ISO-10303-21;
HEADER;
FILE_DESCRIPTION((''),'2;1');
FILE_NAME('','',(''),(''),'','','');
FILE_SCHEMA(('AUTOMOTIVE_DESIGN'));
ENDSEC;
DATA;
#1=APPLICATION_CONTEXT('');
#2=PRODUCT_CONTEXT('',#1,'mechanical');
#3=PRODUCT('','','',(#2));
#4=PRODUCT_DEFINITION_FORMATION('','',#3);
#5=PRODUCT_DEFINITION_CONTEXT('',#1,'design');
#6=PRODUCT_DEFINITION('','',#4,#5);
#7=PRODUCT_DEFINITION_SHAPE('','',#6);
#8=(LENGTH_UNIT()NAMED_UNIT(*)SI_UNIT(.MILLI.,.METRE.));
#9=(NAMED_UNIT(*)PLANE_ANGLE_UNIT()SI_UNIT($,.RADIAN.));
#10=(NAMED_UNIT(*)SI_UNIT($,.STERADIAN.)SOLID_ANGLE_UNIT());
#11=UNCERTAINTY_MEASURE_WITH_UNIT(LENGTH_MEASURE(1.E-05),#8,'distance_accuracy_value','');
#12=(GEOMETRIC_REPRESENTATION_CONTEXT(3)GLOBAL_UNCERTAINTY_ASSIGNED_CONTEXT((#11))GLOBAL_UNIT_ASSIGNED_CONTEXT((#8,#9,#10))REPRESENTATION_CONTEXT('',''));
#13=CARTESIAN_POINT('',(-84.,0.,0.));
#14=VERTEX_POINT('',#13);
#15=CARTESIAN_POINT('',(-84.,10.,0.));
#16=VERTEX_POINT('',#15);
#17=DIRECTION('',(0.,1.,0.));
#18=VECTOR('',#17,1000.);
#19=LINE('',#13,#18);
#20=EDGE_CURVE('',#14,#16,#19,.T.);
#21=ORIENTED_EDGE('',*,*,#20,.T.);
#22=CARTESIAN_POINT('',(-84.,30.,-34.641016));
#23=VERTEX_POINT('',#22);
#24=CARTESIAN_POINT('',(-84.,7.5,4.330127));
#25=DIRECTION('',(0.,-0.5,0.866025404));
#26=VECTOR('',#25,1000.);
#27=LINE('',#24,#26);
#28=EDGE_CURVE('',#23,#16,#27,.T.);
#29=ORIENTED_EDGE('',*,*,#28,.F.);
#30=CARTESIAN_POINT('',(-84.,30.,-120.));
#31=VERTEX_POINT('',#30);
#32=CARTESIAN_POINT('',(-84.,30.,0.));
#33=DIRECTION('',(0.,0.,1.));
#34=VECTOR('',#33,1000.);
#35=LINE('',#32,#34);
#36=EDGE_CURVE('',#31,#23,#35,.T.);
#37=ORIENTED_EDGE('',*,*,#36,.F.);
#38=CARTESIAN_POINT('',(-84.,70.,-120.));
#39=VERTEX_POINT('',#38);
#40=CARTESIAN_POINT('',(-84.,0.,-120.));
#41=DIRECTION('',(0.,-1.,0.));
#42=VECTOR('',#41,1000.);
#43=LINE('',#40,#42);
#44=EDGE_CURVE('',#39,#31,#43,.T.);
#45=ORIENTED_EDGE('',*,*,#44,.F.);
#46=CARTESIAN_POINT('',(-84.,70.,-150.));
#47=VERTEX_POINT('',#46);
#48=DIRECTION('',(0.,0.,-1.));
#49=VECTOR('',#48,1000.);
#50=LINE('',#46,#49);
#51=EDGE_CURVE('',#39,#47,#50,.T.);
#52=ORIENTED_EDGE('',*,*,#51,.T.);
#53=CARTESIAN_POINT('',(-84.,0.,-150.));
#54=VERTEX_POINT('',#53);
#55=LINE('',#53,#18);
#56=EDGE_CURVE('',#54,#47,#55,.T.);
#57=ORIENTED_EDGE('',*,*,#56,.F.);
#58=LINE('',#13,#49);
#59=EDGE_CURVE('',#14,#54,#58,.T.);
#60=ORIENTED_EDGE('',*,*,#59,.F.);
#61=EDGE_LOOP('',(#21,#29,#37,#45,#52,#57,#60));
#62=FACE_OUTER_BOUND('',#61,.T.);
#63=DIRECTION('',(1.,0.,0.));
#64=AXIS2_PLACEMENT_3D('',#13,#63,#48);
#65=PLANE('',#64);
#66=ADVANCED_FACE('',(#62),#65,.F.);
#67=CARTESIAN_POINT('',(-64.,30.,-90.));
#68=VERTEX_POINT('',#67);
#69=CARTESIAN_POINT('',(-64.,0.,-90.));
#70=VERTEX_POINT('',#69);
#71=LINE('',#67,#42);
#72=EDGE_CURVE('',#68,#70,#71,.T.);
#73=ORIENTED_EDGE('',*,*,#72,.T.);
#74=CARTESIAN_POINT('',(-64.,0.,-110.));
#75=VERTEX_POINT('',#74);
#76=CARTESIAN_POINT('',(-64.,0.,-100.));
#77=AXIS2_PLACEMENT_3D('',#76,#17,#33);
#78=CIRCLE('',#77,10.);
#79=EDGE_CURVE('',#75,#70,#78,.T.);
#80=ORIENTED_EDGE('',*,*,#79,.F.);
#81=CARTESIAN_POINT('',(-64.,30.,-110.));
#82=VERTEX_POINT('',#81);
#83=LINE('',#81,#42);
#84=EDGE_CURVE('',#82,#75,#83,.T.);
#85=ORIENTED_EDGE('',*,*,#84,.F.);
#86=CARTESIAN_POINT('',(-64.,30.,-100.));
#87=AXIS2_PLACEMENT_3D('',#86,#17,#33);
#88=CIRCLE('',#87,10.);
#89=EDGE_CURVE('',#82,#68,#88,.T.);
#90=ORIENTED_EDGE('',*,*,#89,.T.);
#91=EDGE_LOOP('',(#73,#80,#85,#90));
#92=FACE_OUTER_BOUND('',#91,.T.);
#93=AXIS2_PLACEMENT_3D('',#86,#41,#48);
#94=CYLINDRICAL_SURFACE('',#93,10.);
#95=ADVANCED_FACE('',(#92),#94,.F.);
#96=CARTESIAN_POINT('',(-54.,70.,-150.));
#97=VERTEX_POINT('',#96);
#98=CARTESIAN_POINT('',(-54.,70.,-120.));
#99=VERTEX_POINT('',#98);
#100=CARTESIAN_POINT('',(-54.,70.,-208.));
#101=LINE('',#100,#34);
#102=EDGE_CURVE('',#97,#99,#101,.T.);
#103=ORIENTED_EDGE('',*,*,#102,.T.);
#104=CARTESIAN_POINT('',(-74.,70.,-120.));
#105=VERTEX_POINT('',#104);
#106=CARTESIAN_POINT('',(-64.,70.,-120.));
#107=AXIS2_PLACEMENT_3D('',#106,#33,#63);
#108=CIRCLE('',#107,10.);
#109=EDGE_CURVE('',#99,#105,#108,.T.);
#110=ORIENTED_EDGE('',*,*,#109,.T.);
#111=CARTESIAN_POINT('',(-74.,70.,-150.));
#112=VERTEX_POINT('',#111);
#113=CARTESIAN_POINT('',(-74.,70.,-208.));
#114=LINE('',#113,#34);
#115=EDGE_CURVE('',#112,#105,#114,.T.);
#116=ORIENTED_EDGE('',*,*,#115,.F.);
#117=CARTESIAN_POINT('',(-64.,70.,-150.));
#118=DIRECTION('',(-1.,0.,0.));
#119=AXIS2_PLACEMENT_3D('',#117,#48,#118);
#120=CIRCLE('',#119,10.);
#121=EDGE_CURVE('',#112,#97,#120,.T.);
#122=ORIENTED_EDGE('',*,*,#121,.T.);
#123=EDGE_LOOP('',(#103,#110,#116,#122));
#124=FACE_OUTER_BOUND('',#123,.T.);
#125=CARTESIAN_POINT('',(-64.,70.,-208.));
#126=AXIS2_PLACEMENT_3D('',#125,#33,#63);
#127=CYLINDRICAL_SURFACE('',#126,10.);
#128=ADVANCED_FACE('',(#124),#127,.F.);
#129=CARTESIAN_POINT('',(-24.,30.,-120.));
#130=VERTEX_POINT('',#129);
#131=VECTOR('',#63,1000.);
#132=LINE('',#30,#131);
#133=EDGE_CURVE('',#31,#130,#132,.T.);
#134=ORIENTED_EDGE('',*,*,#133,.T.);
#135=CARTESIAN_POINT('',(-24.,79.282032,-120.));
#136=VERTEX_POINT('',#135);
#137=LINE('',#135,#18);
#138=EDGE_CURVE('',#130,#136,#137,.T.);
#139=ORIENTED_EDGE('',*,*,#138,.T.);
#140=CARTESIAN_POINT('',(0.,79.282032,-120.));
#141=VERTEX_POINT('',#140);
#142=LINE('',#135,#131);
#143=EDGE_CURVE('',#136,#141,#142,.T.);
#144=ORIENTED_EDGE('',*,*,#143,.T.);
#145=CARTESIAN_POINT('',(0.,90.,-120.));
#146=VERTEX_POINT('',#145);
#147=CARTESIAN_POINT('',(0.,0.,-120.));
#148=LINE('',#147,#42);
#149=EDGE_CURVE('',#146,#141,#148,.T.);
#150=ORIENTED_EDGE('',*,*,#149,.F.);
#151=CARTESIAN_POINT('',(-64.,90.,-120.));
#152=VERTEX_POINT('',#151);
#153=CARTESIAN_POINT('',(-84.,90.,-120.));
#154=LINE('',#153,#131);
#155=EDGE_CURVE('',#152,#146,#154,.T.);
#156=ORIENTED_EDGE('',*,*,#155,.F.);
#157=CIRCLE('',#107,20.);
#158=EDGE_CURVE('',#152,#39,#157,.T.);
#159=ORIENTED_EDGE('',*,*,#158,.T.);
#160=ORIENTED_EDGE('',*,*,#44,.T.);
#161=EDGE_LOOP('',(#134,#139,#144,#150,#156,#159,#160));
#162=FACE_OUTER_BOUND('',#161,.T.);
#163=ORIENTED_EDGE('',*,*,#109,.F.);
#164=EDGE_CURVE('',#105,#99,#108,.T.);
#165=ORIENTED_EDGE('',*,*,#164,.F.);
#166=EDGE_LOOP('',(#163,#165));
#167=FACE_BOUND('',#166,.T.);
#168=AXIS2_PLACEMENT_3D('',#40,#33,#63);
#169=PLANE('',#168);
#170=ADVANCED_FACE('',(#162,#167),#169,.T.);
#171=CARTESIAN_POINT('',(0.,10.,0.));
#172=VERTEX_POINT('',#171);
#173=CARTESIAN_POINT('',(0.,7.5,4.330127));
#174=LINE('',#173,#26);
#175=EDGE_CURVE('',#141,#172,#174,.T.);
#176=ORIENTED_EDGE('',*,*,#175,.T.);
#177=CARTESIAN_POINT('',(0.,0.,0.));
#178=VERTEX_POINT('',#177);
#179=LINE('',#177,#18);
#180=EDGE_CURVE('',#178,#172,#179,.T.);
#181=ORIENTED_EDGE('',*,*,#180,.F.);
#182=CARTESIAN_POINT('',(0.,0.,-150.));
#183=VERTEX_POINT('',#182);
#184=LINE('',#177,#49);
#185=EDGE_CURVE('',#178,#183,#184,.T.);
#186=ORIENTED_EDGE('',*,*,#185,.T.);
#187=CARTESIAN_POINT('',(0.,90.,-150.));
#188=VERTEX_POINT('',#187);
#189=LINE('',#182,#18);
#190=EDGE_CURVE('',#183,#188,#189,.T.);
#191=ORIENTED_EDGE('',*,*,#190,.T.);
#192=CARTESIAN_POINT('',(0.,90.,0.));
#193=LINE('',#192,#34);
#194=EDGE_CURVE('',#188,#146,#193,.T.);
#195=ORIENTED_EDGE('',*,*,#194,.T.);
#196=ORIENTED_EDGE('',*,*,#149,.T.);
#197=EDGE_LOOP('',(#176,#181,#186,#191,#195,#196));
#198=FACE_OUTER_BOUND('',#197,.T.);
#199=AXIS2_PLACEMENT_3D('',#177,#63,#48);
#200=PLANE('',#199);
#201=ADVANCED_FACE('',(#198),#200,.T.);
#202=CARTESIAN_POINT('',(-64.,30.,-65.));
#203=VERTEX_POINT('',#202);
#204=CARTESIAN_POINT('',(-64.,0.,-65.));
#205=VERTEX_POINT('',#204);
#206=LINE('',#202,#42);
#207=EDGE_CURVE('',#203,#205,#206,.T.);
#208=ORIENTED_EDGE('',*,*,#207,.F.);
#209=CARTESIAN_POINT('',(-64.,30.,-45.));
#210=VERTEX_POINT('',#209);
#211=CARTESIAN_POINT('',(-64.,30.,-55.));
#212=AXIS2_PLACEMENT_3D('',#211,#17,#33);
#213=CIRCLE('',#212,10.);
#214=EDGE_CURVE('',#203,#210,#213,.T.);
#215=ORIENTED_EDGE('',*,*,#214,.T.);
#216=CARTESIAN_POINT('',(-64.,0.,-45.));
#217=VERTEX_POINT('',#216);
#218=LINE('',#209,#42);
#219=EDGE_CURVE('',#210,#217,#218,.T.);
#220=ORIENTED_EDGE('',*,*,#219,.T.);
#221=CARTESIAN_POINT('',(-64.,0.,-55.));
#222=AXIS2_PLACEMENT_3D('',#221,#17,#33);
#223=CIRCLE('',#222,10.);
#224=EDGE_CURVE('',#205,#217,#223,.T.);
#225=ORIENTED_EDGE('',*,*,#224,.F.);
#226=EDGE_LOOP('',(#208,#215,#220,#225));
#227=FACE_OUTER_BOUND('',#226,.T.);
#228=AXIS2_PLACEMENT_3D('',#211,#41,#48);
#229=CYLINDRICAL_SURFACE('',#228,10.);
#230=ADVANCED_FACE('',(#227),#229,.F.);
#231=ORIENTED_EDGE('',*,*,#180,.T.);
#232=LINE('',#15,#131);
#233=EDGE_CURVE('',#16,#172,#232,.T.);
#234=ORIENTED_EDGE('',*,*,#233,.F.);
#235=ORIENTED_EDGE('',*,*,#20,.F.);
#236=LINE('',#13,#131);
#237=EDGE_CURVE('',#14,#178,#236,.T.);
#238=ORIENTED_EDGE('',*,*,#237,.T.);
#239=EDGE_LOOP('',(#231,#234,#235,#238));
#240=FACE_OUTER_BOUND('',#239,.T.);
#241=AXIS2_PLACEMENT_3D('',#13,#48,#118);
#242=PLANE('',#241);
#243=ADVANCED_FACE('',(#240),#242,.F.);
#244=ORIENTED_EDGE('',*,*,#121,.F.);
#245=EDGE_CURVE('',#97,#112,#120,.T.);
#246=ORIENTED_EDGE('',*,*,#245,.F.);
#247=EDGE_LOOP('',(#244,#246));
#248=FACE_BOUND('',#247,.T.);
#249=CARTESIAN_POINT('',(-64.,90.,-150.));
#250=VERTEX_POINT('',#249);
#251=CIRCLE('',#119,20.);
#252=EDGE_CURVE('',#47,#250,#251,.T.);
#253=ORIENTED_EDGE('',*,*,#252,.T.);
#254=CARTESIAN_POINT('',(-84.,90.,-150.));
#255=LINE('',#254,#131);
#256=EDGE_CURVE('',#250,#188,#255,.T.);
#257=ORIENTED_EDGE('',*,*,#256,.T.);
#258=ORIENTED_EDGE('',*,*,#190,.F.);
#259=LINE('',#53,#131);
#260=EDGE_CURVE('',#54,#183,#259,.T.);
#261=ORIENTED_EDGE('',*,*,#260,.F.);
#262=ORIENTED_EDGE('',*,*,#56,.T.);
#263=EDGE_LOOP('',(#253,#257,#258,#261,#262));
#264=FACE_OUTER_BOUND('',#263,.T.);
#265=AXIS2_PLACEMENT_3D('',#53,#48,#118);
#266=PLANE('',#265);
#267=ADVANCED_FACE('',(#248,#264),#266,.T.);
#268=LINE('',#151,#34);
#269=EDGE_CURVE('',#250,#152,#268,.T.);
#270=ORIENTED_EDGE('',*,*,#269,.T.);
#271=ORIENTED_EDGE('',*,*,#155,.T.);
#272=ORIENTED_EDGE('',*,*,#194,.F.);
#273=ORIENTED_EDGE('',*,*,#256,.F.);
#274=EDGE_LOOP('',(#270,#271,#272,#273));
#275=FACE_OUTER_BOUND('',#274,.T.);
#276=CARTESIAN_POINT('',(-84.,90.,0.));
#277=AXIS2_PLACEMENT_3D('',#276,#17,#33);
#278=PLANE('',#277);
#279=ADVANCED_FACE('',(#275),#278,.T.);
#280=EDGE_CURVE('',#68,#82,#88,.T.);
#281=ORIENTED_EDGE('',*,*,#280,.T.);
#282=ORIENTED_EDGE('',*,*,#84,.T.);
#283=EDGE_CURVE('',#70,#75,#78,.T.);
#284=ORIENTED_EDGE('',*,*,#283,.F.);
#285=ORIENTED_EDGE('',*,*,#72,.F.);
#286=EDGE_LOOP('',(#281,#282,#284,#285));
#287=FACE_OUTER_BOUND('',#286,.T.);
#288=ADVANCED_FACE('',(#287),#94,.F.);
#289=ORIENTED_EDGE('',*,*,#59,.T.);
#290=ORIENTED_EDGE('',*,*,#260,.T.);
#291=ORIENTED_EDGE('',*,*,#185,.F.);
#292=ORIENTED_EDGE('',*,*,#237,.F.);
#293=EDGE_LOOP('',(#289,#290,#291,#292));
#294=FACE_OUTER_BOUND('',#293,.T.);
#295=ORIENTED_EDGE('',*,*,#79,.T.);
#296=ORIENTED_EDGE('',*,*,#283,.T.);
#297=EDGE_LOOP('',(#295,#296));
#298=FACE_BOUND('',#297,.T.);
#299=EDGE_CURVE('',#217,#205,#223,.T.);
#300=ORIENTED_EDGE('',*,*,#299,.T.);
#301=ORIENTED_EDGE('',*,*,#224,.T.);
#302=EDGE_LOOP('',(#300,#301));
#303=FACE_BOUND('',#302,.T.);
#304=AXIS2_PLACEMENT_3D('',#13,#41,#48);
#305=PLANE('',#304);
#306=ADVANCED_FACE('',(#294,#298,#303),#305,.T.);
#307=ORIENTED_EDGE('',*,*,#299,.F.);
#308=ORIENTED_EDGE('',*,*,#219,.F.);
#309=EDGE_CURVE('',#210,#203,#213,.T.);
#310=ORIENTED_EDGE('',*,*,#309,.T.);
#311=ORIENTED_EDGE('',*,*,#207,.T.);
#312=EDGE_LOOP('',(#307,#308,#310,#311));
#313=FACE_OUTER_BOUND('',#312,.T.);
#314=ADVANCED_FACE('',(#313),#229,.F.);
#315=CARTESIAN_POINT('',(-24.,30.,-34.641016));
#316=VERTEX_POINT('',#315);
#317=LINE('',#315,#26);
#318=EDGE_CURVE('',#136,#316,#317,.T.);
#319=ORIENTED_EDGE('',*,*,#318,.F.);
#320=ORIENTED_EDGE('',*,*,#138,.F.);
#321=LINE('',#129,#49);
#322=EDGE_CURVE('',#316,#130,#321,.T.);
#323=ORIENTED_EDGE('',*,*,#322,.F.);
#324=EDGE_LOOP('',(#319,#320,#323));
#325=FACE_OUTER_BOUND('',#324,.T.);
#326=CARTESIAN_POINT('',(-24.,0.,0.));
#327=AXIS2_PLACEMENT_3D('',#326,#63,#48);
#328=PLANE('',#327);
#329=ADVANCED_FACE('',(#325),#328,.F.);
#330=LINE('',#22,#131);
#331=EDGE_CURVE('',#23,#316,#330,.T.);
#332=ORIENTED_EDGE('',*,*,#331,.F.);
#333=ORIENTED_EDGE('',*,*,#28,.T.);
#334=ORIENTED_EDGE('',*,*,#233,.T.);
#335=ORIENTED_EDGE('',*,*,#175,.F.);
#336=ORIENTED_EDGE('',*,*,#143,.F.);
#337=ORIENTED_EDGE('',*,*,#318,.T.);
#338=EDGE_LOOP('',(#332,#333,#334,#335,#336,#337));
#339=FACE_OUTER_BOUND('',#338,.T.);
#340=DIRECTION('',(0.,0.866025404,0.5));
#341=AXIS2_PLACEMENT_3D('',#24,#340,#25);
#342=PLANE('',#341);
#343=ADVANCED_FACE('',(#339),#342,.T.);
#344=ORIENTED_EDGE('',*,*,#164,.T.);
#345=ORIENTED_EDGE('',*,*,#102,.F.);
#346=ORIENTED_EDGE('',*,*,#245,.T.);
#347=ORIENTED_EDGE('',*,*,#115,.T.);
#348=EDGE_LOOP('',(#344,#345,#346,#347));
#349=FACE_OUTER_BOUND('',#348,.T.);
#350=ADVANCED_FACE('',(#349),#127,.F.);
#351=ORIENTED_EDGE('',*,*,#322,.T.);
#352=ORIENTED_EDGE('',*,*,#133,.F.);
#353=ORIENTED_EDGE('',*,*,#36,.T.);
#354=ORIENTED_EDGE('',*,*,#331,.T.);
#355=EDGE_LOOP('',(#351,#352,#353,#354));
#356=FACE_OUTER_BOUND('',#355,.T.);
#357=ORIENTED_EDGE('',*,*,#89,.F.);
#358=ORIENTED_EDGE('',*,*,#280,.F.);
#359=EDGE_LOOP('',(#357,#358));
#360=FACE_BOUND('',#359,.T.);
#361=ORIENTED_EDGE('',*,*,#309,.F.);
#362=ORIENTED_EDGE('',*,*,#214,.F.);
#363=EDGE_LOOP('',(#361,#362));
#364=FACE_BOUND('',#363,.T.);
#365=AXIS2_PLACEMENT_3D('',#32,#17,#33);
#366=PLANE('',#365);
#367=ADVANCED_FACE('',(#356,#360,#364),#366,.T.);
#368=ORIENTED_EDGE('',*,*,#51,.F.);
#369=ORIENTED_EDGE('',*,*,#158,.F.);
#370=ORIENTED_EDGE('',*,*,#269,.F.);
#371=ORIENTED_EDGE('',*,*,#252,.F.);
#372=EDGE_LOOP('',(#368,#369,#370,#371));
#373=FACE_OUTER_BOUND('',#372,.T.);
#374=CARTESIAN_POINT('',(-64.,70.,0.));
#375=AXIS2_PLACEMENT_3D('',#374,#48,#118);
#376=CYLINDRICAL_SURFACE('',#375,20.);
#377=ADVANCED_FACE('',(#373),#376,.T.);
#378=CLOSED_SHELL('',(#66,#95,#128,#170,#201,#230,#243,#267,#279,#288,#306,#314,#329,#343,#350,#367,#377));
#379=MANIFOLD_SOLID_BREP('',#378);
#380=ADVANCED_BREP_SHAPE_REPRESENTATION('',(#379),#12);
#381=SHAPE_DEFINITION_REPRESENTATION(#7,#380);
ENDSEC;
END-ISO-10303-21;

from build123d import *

# Parameters (mm, degrees)
BRACKET_BODY_DEPTH     = 84
GUSSET_DEPTH           = 24
BASE_HOLES_SKETCH_R    = 10
BASE_HOLES_2X_20_DEPTH = 30
LUG_HOLE_SKETCH_R      = 10
LUG_HOLE_20_DEPTH      = 208
LUG_TOP_FILLET_R20_R   = 20


with BuildPart() as part:
    # Bracket Profile Sketch → Bracket Body (new body)
    with BuildSketch(Plane(origin=(0, 0, 0), x_dir=(0, 0, -1), z_dir=(1, 0, 0))):
        Polygon((0, 10), (0, 0), (150, 0), (150, 90), (120, 90), (120, 79.282032303), (120, 70), (120, 30), (34.641016151, 30), align=None)
    extrude(amount=-BRACKET_BODY_DEPTH)

    # Gusset Sketch → Gusset (add)
    with BuildSketch(Plane(origin=(0, 0, 0), x_dir=(0, 0, -1), z_dir=(1, 0, 0))):
        Polygon((34.641016151, 30), (120, 79.282032303), (120, 30), align=None)
    extrude(amount=-GUSSET_DEPTH)

    # Base Holes Sketch → Base Holes 2xØ20 (cut)
    with BuildSketch(Plane(origin=(0, 0, 0), x_dir=(1, 0, 0), z_dir=(0, 1, 0))):
        with Locations(Location((-64, 100, 0), (0, 0, 270))):
            Circle(BASE_HOLES_SKETCH_R)
        with Locations(Location((-64, 55, 0), (0, 0, 270))):
            Circle(BASE_HOLES_SKETCH_R)
    extrude(amount=BASE_HOLES_2X_20_DEPTH, mode=Mode.SUBTRACT)

    # Lug Hole Sketch → Lug Hole Ø20 (cut)
    with BuildSketch(Plane.XY):
        with Locations((-64, 70)):
            Circle(LUG_HOLE_SKETCH_R)
    extrude(amount=-LUG_HOLE_20_DEPTH, mode=Mode.SUBTRACT)

    # Lug Top Fillet R20
    lug_top_fillet_r20_edges = [part.edges().sort_by_distance(p)[0] for p in [
        (-84, 90, -135),
    ]]
    fillet(lug_top_fillet_r20_edges, radius=LUG_TOP_FILLET_R20_R)


solid = part.part
